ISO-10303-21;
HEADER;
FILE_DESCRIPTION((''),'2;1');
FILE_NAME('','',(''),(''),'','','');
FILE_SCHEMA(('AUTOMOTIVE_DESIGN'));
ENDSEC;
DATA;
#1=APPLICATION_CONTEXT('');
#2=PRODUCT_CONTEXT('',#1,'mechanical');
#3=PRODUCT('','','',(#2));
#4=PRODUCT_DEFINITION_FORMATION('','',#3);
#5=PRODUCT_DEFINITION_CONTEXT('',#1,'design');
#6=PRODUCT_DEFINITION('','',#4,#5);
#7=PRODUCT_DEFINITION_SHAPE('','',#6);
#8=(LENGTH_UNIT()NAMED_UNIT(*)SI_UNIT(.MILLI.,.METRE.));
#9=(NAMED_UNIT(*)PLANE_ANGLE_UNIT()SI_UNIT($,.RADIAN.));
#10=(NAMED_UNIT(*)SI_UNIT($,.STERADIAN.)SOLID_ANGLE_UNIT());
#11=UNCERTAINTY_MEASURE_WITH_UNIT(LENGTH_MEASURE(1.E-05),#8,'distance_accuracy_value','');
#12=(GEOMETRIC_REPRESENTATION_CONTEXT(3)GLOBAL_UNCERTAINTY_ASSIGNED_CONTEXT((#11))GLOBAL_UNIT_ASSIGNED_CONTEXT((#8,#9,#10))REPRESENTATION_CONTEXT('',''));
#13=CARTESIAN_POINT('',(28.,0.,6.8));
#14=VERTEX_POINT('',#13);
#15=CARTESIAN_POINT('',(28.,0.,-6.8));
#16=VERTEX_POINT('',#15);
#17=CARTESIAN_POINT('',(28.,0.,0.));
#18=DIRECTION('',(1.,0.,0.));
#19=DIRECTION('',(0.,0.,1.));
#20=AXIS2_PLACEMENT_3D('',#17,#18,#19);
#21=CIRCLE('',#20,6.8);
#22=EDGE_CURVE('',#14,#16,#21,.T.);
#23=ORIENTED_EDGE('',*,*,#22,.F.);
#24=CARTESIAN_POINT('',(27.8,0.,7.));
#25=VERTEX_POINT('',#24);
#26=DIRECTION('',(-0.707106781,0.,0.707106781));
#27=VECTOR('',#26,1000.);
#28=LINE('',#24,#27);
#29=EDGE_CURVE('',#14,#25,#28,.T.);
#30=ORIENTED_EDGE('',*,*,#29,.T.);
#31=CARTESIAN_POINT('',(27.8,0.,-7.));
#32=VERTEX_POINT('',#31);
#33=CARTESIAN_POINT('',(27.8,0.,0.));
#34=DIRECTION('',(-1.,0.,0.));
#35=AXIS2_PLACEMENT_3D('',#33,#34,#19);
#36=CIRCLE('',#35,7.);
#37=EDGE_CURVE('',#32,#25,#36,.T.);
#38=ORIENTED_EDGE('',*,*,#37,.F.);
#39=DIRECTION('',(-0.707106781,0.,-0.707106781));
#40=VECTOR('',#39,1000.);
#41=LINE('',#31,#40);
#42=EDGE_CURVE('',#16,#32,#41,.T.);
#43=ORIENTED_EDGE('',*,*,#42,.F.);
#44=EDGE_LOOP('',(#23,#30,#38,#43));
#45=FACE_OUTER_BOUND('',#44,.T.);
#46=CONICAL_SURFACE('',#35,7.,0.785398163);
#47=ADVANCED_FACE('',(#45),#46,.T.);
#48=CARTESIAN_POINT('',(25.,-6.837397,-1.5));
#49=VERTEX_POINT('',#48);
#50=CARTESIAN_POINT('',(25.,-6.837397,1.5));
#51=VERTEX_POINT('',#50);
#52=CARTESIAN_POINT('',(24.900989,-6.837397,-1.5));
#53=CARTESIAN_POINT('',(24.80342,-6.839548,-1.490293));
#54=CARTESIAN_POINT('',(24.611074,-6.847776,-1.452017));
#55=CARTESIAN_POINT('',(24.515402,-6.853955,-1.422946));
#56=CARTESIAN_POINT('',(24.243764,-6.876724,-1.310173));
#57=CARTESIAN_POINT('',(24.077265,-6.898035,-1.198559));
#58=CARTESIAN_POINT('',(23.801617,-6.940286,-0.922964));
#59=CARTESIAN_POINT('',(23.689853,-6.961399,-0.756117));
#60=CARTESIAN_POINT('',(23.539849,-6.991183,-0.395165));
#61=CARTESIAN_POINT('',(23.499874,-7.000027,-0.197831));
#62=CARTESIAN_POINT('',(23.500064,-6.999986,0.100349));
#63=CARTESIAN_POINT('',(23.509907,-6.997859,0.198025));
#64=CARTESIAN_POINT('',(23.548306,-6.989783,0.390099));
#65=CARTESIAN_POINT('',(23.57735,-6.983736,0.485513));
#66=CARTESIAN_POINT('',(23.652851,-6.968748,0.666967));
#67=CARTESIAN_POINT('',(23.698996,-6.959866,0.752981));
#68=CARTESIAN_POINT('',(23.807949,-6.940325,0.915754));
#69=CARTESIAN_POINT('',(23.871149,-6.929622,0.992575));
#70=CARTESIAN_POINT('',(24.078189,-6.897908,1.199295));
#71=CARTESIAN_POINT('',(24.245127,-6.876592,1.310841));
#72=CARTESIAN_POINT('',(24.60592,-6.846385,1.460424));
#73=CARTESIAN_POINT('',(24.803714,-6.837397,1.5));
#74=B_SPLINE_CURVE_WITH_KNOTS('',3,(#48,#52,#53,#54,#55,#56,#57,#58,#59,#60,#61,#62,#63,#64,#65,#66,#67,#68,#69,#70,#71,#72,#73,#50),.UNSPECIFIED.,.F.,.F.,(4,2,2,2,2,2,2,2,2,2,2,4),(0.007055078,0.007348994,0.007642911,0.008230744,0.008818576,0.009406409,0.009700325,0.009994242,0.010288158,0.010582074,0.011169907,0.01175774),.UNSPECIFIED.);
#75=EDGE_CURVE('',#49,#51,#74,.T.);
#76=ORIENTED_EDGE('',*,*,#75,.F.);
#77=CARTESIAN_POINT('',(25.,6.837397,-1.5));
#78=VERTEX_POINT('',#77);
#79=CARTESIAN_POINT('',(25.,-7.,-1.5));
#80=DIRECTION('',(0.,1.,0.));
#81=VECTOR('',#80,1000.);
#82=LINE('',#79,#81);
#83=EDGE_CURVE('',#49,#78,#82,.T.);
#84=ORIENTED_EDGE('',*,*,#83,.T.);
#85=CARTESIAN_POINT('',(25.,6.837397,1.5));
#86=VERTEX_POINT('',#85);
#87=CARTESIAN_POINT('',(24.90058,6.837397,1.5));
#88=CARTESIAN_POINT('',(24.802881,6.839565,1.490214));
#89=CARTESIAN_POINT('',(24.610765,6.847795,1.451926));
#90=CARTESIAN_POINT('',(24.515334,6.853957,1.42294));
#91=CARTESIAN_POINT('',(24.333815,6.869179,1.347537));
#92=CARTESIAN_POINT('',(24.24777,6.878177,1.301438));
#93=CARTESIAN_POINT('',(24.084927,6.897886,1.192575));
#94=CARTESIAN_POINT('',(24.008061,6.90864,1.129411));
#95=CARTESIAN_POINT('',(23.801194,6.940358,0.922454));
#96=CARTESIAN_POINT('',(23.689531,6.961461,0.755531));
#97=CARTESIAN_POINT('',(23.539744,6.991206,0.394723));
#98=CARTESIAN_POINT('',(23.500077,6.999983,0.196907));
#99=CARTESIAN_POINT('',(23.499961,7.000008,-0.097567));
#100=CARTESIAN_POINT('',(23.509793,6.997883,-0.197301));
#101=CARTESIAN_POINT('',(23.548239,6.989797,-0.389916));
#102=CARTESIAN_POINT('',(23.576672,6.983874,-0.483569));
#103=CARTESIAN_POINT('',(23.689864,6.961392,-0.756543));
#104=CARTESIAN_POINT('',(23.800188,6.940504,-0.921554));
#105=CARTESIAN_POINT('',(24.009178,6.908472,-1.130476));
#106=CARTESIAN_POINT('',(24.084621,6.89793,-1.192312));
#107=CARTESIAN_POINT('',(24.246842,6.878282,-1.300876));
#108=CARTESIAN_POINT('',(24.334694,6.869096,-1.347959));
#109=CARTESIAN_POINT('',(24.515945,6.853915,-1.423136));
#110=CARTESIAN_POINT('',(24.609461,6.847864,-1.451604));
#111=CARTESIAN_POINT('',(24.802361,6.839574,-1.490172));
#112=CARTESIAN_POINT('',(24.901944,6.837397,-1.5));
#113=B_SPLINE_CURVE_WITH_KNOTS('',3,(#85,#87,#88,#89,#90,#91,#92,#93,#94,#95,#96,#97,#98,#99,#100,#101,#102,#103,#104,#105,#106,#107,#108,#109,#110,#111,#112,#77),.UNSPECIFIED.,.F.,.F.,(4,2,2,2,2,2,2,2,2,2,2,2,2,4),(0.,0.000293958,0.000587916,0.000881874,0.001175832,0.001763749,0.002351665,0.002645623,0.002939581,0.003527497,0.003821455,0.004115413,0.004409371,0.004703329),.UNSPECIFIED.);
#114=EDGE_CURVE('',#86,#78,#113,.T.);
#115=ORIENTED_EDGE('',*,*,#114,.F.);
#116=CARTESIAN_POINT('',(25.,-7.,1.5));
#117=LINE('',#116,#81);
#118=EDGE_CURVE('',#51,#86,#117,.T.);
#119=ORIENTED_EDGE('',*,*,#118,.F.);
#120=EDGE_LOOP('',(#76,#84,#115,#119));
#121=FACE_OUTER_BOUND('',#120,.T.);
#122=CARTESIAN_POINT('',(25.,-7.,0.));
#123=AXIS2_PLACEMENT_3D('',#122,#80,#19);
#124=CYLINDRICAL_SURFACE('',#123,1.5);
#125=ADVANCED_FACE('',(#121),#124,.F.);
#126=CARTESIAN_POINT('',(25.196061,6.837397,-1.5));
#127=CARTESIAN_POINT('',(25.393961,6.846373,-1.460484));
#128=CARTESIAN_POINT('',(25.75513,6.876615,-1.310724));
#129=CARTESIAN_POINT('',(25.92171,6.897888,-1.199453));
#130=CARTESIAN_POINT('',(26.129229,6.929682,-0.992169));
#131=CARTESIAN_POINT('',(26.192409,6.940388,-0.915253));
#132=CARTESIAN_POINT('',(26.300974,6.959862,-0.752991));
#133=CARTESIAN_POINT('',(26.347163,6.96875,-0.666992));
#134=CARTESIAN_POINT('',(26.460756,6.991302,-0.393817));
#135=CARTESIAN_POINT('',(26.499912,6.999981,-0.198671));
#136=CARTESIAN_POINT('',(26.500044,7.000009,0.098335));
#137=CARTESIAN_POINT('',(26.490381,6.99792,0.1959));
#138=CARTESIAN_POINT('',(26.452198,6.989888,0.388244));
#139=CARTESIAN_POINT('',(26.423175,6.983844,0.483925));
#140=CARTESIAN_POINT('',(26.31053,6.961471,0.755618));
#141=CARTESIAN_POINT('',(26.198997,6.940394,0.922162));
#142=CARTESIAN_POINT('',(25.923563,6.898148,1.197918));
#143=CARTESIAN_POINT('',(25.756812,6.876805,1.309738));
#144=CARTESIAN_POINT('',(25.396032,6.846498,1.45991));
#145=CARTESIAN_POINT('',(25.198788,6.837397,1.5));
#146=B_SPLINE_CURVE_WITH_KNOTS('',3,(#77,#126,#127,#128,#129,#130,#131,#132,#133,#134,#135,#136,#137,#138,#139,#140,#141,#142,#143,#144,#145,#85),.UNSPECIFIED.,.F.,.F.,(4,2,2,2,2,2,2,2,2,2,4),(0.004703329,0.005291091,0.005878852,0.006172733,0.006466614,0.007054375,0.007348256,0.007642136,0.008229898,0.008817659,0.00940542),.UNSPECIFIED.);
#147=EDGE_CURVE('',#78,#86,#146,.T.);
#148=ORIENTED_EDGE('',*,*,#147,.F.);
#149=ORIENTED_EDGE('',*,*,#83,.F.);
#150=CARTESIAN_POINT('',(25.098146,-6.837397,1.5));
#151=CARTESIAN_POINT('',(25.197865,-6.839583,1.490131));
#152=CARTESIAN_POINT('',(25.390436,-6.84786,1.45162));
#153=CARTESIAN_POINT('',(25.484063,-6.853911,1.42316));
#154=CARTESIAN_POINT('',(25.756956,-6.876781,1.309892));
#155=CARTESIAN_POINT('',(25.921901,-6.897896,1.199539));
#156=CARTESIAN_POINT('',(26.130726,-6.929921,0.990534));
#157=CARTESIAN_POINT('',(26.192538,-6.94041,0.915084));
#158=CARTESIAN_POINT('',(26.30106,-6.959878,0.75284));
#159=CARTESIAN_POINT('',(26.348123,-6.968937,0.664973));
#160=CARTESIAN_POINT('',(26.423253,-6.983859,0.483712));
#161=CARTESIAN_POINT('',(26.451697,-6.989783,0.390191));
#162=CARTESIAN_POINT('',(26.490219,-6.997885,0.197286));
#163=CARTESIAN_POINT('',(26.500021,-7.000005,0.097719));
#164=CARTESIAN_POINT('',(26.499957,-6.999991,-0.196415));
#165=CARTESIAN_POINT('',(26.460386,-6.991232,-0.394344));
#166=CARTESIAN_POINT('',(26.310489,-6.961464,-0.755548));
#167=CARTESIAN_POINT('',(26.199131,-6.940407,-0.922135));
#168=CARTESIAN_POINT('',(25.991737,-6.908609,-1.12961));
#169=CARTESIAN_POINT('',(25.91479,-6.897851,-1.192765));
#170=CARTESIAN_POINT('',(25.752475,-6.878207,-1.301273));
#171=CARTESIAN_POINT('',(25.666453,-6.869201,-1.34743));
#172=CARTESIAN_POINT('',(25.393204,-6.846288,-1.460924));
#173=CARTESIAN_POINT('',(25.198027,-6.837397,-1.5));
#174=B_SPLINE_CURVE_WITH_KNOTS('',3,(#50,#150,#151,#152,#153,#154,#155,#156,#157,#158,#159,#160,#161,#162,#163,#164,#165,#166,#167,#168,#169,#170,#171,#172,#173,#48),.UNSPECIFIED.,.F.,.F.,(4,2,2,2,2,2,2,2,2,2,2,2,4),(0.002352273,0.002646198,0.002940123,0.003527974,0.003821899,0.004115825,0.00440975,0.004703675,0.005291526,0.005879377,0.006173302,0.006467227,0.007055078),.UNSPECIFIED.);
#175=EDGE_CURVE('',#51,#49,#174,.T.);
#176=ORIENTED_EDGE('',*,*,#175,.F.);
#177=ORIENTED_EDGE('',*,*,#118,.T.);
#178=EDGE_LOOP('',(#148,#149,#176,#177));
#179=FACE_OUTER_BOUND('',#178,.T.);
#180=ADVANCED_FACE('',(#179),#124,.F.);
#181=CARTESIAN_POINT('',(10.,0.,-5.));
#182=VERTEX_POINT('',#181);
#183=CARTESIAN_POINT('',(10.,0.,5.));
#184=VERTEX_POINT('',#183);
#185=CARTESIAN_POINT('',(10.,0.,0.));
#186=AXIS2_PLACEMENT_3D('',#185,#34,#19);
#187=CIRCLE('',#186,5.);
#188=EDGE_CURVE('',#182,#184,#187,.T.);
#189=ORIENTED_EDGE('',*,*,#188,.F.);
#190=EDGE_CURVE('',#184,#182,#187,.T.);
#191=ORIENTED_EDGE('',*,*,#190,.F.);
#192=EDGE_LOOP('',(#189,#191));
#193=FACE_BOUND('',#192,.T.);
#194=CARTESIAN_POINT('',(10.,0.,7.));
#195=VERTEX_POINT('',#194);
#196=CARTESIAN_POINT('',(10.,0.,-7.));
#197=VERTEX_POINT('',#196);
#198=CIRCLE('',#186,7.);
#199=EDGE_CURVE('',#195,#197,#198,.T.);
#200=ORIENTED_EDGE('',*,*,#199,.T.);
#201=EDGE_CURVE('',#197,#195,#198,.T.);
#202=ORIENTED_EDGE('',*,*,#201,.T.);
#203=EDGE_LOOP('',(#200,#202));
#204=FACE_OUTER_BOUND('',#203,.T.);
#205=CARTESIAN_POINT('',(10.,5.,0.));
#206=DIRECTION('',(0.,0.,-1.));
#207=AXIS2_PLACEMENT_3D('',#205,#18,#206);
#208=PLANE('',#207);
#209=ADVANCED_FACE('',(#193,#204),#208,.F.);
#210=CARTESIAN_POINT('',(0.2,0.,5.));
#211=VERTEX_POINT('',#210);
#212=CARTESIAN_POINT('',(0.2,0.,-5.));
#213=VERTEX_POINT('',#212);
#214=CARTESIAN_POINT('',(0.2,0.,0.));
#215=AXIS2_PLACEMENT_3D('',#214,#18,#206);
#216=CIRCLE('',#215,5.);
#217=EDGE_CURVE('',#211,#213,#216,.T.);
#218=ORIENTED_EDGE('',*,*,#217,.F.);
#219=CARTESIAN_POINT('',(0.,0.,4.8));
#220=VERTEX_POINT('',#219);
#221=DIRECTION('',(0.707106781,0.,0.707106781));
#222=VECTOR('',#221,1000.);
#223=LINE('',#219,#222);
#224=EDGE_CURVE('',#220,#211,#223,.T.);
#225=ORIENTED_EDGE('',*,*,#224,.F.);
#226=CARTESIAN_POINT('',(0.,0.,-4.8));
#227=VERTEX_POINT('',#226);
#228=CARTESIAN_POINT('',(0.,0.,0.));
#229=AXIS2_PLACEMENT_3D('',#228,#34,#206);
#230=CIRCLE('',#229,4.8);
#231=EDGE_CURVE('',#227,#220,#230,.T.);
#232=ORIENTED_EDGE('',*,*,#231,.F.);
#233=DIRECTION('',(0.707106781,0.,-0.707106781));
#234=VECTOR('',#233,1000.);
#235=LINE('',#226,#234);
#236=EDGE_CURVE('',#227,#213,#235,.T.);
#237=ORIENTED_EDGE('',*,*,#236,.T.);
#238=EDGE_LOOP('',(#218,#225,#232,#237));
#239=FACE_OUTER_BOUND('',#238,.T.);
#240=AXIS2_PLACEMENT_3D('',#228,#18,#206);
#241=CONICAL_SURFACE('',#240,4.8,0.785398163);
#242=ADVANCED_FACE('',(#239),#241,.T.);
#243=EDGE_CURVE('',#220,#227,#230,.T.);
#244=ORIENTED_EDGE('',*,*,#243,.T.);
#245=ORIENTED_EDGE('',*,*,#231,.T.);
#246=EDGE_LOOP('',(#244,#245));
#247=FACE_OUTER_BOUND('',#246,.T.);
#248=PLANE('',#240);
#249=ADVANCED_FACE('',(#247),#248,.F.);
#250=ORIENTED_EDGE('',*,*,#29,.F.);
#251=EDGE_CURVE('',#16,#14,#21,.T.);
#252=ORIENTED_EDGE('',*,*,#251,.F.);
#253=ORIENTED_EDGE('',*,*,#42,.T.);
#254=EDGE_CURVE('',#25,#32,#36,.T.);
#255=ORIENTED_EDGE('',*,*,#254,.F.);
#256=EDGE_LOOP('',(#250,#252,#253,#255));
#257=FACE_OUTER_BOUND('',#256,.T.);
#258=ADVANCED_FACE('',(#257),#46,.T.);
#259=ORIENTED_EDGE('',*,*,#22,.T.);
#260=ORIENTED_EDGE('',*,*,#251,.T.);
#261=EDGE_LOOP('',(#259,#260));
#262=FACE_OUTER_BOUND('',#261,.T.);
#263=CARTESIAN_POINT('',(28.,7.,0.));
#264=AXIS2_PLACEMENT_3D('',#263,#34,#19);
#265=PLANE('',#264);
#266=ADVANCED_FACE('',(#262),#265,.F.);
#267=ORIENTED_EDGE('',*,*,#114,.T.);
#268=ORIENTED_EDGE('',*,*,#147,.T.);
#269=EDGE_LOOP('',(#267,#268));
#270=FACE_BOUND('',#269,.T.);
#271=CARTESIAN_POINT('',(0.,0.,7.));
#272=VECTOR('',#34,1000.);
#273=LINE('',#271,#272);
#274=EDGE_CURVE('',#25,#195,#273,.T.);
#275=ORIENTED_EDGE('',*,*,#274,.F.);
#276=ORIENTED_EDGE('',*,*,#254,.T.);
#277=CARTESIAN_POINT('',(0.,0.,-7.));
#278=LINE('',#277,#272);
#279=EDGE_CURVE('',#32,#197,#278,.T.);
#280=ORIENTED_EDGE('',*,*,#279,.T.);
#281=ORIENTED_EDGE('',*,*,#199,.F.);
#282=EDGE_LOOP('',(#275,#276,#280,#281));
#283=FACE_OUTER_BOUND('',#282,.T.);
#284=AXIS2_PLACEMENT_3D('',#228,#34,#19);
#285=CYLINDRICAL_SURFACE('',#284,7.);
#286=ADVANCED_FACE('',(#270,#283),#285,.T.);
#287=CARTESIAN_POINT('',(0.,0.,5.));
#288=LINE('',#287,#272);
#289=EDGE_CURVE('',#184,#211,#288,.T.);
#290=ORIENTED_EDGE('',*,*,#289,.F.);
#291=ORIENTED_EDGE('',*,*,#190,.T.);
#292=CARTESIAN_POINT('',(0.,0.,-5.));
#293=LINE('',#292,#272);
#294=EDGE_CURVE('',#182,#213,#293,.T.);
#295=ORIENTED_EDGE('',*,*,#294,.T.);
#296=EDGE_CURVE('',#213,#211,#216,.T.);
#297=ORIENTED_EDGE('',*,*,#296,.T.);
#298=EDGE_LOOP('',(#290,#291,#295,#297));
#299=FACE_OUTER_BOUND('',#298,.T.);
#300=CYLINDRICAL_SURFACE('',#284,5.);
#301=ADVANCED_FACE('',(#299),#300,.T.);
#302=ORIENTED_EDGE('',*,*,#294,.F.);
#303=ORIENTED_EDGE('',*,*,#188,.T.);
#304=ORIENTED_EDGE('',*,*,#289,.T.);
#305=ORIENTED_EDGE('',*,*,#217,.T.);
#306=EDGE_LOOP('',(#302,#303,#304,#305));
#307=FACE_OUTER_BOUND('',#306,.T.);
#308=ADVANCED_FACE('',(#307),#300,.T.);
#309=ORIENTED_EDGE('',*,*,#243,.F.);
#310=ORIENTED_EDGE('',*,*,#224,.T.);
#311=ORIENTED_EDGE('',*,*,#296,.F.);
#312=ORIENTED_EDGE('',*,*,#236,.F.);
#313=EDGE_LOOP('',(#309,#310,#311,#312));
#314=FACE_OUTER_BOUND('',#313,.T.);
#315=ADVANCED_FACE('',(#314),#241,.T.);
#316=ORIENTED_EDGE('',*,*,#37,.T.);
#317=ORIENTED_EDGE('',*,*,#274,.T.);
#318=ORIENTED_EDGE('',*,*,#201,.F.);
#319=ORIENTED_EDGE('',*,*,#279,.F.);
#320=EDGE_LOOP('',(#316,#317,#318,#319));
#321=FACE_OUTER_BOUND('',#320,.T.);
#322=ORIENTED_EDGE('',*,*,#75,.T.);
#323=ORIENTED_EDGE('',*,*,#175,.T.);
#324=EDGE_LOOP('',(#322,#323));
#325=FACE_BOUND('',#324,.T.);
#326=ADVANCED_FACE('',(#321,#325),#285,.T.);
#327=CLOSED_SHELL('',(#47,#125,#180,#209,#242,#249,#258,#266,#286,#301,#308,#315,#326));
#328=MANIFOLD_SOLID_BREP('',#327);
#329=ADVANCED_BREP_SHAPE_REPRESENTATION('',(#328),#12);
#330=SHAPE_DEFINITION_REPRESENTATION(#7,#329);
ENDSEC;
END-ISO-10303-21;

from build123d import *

# Parameters (mm, degrees)
CHAMFER1_SIZE           = 0.2
CUT_EXTRUDE2_DEPTH      = 30.69848481
CUT_EXTRUDE2_DEPTH_BACK = 30.69848481
SKETCH3_R               = 1.5
CHAMFER2_SIZE           = 0.2


with BuildPart() as part:
    # Sketch1 → Revolve1 (revolve)
    with BuildSketch(Plane.XY, mode=Mode.PRIVATE) as revolve1_sk:
        Polygon((0, 0), (0, 5), (10, 5), (10, 7), (28, 7), (28, 0), align=None)
    revolve(revolve1_sk.sketch.rotate(Axis((0, 0, 0), (1, 0, 0)), 90), axis=Axis((0, 0, 0), (1, 0, 0)))

    # Chamfer1
    chamfer1_edges = [part.edges().sort_by_distance(p)[0] for p in [
        (0, 0, -5),
    ]]
    chamfer(chamfer1_edges, length=CHAMFER1_SIZE)

    # Sketch3 → Cut-Extrude2 (cut, two sides: drawn at the far end of the back side and taken through both)
    with BuildSketch(Plane(origin=(0, 0, 0), x_dir=(1, 0, 0), z_dir=(0, 1, 0)).offset(-CUT_EXTRUDE2_DEPTH_BACK)):
        with Locations(Location((25, 0, 0), (0, 0, 270))):
            Circle(SKETCH3_R)
    extrude(amount=CUT_EXTRUDE2_DEPTH + CUT_EXTRUDE2_DEPTH_BACK, mode=Mode.SUBTRACT)

    # Chamfer2
    chamfer2_edges = [part.edges().sort_by_distance(p)[0] for p in [
        (28, 0, -7),
    ]]
    chamfer(chamfer2_edges, length=CHAMFER2_SIZE)


solid = part.part
